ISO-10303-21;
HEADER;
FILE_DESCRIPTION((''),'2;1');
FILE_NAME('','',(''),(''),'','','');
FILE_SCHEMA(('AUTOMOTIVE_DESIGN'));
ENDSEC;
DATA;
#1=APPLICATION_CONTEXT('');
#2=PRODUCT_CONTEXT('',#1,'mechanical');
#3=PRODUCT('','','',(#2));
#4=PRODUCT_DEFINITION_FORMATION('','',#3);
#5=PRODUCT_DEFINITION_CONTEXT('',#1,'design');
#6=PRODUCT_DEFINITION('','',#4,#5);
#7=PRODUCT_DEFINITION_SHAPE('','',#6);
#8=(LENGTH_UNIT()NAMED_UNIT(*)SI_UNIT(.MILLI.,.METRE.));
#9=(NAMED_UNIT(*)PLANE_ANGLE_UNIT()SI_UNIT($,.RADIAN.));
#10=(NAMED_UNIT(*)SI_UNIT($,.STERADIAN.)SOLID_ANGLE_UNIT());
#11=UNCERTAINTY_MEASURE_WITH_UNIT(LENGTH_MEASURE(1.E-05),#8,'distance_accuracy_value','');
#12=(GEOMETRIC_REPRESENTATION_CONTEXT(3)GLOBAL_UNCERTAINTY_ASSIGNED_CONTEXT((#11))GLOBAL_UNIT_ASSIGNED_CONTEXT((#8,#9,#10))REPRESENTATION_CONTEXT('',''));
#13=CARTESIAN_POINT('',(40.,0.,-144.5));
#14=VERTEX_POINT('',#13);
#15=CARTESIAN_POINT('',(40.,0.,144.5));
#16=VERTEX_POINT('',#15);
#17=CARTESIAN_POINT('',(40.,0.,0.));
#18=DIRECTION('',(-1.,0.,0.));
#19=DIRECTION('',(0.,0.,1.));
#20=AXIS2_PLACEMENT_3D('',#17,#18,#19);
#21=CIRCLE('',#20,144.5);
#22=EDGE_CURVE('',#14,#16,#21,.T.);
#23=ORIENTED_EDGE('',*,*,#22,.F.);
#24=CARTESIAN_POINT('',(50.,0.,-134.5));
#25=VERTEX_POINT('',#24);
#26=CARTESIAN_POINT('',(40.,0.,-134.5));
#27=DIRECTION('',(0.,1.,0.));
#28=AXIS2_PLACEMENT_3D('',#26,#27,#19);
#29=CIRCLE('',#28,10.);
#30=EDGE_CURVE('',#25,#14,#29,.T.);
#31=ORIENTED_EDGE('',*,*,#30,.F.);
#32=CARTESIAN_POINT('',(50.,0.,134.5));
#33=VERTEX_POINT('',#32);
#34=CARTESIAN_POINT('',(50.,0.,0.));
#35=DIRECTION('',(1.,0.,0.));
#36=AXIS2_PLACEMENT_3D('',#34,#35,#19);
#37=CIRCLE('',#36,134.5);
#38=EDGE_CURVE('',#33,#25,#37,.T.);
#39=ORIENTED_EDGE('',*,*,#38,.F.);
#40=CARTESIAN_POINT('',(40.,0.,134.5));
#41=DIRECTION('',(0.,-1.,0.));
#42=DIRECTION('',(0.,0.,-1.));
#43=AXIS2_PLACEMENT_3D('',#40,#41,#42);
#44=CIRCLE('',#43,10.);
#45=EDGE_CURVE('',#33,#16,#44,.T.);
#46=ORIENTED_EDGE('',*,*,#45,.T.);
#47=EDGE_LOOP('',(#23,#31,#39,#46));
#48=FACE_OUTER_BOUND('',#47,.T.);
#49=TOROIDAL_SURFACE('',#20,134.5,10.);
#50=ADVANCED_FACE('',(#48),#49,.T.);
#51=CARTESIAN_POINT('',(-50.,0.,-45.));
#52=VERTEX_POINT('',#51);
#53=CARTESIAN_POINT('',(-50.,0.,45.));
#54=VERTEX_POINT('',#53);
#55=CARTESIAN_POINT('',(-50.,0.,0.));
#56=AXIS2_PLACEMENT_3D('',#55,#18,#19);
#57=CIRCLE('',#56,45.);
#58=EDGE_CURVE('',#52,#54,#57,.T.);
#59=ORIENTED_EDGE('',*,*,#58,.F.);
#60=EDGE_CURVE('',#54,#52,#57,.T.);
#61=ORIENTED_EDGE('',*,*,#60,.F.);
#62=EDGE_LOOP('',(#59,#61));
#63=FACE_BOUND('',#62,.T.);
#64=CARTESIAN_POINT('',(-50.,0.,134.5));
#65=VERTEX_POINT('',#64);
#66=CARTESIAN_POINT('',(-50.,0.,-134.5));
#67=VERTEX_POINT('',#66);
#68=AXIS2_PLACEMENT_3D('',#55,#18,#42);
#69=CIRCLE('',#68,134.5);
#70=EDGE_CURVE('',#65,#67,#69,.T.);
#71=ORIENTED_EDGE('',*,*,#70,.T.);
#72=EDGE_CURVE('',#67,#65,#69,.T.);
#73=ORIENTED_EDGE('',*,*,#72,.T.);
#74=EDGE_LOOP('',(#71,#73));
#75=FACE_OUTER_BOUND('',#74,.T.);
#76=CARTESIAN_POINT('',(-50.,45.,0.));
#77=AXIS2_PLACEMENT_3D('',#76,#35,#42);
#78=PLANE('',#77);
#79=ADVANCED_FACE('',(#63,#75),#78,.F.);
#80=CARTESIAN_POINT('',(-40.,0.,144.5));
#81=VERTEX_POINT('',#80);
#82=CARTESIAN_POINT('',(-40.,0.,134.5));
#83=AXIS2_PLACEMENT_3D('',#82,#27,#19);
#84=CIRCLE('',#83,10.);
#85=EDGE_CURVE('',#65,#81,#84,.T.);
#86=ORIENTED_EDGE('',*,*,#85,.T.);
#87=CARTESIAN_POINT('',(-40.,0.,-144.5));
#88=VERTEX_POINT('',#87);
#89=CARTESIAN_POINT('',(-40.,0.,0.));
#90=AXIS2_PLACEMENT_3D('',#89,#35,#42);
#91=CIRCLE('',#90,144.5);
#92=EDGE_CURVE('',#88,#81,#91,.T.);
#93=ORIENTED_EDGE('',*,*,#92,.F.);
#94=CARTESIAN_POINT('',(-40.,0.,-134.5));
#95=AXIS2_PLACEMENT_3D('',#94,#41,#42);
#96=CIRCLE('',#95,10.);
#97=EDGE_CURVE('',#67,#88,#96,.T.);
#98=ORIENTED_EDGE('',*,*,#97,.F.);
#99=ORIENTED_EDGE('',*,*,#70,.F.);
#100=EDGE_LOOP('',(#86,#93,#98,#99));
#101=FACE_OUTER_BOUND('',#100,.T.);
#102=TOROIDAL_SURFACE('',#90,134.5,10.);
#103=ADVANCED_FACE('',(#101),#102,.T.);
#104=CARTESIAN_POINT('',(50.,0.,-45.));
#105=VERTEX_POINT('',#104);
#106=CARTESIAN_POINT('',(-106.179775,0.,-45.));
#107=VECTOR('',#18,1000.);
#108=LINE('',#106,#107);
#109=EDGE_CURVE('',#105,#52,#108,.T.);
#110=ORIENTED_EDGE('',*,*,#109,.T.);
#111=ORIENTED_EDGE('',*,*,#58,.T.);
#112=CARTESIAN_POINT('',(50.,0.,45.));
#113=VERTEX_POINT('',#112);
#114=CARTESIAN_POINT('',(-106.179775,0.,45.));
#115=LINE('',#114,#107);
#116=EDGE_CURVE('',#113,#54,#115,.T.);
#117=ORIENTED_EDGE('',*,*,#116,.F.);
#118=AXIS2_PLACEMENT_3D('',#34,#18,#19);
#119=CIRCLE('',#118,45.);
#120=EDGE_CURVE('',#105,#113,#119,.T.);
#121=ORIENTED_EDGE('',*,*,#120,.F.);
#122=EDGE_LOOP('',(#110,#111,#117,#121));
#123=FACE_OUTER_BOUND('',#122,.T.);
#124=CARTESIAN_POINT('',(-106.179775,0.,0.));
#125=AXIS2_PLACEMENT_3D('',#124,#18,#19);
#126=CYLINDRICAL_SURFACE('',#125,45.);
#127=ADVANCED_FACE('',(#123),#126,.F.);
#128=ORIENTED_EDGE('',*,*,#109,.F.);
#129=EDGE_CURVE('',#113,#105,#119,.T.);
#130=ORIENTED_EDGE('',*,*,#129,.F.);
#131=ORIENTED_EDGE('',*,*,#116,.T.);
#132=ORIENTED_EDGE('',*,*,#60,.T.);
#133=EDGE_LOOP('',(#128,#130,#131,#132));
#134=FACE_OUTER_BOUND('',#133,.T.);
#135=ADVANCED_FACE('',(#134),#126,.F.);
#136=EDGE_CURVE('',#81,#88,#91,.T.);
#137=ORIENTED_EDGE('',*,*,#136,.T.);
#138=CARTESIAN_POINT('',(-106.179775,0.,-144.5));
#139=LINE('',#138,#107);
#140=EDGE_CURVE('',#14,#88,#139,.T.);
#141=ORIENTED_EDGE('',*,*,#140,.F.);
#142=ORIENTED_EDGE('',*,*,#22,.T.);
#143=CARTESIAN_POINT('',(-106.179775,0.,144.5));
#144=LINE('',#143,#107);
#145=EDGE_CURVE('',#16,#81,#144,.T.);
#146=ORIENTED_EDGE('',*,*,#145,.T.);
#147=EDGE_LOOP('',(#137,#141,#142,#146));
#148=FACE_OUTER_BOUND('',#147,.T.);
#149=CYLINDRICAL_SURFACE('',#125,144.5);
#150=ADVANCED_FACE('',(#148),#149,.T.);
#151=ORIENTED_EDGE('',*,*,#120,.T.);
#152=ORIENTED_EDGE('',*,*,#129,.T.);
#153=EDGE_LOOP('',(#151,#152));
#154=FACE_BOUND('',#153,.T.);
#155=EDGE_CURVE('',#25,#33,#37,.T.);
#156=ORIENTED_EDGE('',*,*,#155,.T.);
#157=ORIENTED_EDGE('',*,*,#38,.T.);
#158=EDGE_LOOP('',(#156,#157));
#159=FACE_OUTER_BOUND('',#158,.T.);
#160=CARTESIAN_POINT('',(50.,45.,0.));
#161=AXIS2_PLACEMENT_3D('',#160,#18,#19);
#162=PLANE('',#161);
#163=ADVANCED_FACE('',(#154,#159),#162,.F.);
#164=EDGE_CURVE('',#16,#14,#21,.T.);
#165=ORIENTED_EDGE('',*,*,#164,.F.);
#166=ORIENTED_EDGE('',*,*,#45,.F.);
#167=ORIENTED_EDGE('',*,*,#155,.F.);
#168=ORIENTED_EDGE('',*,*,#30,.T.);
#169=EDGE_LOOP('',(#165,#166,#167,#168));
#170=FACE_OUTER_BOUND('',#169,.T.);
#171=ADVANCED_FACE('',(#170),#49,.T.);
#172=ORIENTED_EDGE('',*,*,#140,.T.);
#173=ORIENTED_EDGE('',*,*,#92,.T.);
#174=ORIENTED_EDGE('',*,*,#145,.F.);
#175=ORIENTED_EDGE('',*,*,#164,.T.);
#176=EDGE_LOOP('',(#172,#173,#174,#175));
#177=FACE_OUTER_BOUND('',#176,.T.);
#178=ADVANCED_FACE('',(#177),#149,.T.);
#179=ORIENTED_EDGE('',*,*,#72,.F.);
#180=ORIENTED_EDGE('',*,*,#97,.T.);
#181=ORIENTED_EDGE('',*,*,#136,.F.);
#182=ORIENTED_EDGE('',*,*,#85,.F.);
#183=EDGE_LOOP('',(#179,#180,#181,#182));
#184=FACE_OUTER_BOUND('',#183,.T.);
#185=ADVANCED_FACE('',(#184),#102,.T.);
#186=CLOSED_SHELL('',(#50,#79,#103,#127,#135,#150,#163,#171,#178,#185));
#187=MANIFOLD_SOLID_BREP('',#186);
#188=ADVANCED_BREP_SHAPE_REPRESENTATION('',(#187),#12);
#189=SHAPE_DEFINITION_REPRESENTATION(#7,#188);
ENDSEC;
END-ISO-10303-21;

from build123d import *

# Parameters (mm, degrees)
SKETCH_1_W = 100
SKETCH_1_H = 99.5
FILLET_1_R = 10


with BuildPart() as part:
    # Sketch 1 → Revolve 1 (revolve)
    with BuildSketch(Plane.XY, mode=Mode.PRIVATE) as revolve_1_sk:
        with Locations((0, 94.75)):
            Rectangle(SKETCH_1_W, SKETCH_1_H)
    revolve(revolve_1_sk.sketch.rotate(Axis((-106.179775281, 0, 0), (1, 0, 0)), 90), axis=Axis((-106.179775281, 0, 0), (1, 0, 0)))

    # Fillet 1
    fillet_1_edges = [part.edges().sort_by_distance(p)[0] for p in [
        (50, 0, -144.5),
        (-50, 0, -144.5),
    ]]
    fillet(fillet_1_edges, radius=FILLET_1_R)


solid = part.part
